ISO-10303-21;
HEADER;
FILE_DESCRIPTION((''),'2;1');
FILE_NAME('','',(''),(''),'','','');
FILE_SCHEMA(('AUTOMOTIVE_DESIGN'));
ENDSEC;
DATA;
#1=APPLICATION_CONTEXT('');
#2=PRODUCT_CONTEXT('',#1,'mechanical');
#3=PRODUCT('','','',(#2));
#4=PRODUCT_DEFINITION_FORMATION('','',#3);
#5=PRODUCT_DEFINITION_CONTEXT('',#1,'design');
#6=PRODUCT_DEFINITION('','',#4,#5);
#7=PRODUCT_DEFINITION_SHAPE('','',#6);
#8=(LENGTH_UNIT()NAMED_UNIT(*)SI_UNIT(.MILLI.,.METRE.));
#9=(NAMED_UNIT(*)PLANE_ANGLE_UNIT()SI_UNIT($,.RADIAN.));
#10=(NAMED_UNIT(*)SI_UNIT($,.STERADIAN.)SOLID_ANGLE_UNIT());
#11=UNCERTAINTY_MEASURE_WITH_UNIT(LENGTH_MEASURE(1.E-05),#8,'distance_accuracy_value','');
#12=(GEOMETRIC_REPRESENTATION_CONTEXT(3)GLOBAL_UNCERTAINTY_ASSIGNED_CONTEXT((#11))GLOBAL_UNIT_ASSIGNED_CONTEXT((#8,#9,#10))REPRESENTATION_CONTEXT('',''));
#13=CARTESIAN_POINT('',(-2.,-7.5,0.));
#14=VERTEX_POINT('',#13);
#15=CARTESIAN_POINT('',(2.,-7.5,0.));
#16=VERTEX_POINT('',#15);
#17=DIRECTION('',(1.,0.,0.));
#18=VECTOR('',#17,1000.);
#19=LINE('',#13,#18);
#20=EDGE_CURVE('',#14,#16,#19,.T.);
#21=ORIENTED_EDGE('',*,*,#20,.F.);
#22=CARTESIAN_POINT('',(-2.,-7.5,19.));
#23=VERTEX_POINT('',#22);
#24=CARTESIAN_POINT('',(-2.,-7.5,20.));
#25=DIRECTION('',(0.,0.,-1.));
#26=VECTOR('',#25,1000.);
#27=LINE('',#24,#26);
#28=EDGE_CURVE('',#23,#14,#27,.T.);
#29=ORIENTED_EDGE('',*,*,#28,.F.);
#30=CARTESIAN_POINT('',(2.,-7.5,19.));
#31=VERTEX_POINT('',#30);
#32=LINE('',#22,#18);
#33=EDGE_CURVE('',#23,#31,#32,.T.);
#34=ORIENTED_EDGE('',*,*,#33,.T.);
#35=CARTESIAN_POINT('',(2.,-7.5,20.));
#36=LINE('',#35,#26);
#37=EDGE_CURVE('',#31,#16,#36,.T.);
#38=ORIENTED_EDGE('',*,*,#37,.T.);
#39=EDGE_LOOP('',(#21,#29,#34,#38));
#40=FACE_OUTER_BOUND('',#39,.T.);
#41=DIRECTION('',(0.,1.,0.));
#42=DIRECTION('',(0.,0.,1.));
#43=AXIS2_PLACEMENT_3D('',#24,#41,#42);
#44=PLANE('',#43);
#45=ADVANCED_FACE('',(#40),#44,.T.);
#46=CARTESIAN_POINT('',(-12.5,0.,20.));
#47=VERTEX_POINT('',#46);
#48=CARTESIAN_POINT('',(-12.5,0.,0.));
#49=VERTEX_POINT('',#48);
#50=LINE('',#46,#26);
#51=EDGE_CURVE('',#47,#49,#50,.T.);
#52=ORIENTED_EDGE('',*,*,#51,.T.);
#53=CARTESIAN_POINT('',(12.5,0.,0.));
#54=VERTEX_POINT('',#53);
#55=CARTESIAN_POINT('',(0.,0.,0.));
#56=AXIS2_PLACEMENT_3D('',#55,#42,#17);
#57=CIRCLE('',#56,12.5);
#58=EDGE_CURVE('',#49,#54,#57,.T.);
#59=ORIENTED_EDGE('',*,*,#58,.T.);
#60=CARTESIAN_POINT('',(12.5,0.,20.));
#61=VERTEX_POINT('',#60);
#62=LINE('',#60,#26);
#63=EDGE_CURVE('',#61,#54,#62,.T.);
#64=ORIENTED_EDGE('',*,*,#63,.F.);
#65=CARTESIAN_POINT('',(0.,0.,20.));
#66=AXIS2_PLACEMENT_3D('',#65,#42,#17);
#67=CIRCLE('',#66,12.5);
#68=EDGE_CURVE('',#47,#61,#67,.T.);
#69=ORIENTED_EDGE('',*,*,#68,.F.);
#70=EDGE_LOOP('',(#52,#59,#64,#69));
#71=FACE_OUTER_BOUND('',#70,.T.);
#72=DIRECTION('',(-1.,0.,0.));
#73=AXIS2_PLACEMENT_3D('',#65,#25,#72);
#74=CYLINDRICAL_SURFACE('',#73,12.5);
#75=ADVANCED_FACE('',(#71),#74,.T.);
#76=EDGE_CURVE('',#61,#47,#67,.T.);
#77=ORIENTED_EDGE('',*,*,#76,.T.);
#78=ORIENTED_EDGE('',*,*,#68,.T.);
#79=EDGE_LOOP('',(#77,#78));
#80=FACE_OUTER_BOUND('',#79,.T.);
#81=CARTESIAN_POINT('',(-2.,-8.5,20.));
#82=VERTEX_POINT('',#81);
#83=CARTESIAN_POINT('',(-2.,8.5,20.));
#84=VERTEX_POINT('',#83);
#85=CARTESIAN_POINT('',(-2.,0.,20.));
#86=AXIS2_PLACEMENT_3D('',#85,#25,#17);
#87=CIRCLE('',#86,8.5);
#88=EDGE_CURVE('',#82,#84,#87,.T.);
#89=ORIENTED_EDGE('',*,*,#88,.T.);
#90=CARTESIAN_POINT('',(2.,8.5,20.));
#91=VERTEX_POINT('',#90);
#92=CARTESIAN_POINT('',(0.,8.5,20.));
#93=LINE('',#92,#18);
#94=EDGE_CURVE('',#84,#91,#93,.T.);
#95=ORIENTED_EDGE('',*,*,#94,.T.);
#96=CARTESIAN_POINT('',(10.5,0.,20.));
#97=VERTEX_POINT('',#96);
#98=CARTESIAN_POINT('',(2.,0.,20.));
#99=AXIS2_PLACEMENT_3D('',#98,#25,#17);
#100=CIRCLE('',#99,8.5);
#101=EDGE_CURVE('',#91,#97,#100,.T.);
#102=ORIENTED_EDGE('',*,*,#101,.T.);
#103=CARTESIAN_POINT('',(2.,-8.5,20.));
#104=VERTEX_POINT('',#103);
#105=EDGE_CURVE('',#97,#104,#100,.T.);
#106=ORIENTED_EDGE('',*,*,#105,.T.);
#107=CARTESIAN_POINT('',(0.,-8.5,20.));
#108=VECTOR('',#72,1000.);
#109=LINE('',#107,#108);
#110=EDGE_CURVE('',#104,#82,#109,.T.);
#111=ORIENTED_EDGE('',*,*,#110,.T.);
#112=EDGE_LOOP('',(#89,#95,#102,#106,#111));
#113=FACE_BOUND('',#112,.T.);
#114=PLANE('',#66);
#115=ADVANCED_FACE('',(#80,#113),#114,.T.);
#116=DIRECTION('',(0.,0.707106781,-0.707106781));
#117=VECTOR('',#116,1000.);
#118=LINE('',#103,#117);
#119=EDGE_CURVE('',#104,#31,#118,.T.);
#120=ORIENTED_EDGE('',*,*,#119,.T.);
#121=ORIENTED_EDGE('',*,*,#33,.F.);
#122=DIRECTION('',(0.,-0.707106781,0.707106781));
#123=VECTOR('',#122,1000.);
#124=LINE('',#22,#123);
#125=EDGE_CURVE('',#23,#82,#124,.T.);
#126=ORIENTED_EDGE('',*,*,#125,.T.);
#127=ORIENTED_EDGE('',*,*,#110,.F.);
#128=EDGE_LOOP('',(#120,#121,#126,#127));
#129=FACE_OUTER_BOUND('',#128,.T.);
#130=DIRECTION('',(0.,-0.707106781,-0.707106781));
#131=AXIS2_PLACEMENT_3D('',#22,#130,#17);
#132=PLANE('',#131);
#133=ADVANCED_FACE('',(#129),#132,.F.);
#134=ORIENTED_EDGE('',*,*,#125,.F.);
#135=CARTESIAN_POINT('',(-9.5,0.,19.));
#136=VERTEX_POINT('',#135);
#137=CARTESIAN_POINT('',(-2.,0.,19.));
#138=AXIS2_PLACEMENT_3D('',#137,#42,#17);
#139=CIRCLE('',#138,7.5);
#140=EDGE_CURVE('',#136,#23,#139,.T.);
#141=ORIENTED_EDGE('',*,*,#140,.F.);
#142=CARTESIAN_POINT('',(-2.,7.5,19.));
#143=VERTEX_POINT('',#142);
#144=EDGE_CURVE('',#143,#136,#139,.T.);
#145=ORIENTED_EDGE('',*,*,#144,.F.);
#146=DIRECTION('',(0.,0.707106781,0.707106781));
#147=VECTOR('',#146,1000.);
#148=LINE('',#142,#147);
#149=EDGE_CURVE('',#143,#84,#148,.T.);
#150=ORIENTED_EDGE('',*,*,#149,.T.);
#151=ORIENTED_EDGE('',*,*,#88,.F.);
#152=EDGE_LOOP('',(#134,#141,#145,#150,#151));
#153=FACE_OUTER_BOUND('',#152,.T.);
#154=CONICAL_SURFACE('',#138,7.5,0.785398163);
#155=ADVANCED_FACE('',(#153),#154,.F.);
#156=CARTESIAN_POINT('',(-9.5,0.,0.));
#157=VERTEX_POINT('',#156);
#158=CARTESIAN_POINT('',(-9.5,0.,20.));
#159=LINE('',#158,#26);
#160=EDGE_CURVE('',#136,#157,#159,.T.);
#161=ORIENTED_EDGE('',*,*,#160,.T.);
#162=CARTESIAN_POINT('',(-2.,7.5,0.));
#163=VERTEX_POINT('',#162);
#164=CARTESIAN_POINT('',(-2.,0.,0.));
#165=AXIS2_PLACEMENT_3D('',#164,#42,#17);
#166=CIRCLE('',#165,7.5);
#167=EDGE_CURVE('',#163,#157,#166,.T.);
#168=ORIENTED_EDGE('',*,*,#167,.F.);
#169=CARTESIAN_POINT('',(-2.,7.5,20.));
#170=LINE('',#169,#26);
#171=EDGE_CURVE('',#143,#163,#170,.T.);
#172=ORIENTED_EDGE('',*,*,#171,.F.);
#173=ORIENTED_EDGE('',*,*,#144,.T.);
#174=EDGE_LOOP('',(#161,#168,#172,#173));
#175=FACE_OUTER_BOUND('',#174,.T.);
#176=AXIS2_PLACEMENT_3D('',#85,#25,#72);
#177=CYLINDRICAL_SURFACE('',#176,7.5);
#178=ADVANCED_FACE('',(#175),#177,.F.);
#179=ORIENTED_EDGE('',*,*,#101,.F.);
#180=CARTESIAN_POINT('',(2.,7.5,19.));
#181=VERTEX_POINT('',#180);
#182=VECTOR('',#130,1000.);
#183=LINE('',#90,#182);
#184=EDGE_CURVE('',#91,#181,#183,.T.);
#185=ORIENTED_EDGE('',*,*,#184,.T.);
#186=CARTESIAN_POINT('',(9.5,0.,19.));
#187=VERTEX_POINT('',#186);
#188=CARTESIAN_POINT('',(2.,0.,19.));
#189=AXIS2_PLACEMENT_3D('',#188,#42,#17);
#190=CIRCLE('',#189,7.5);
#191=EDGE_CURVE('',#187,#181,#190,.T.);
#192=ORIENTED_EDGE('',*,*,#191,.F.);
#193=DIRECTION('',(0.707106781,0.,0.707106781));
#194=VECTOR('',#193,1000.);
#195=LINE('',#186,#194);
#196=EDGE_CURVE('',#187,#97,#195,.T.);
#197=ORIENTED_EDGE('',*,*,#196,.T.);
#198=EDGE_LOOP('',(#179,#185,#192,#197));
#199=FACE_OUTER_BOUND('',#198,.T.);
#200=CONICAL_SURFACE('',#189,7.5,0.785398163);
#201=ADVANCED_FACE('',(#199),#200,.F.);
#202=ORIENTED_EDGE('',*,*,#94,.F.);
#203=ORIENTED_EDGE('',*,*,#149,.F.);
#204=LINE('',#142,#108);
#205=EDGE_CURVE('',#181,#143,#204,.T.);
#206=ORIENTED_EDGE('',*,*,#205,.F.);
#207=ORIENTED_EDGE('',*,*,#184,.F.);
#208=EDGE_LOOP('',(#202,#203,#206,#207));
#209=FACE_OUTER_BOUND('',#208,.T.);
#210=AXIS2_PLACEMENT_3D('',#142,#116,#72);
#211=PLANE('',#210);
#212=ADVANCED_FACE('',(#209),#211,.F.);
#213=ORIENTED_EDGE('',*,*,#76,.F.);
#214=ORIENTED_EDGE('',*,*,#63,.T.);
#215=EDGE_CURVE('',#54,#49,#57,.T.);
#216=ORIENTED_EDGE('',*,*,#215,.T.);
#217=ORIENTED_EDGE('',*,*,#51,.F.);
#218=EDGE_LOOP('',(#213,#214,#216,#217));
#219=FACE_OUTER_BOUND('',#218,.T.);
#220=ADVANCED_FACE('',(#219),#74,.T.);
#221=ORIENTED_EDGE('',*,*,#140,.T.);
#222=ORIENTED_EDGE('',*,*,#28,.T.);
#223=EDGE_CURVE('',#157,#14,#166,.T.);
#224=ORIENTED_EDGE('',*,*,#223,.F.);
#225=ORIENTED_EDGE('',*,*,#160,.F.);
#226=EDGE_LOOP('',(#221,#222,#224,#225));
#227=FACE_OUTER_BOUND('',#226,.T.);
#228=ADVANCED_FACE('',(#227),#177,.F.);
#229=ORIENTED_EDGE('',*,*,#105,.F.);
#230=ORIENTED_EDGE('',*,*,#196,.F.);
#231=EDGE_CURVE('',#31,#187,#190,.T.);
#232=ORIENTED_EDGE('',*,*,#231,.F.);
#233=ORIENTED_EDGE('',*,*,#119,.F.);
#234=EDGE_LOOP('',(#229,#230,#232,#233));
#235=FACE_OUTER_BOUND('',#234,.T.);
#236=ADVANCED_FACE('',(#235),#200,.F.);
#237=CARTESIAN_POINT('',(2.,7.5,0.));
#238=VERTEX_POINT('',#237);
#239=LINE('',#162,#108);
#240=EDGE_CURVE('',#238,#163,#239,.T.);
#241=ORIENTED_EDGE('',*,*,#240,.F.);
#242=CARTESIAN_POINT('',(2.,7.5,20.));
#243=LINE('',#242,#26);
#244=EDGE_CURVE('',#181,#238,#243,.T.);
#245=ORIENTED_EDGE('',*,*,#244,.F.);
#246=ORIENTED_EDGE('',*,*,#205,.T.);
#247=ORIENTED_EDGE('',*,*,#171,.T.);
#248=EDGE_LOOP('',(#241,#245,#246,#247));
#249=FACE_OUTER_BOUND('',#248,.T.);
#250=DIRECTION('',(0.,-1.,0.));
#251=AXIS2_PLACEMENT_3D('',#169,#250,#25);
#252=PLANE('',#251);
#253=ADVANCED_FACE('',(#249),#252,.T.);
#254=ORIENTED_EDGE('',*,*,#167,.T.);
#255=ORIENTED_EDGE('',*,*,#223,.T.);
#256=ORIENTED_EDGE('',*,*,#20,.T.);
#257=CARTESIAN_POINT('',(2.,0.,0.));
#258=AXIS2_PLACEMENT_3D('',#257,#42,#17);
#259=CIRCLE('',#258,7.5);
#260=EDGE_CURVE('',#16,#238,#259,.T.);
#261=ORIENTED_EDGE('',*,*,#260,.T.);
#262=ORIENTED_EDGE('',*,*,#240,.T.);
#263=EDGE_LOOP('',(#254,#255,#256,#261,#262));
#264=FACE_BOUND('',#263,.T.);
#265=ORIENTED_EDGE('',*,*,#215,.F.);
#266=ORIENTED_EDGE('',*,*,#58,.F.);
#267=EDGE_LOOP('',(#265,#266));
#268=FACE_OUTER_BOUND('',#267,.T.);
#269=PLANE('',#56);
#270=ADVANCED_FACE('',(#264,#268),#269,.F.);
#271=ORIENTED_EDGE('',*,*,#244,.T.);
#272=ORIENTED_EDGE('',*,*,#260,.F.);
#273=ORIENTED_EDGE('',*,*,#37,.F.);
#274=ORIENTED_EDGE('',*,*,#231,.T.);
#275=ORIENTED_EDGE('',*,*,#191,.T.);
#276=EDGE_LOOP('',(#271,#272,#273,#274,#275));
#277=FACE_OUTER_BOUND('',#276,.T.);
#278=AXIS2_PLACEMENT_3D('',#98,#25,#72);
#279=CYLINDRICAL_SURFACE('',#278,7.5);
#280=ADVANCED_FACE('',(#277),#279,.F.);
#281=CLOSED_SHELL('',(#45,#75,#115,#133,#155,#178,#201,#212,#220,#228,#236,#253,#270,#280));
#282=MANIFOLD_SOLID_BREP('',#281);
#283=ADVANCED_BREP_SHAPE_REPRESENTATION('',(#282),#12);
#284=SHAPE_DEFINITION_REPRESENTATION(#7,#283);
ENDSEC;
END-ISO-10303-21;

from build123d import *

# Parameters (mm, degrees)
SKETCH1_R           = 12.5
BOSS_EXTRUDE1_DEPTH = 20
CHAMFER1_SIZE       = 1


with BuildPart() as part:
    # Sketch1 → Boss-Extrude1 (new body)
    with BuildSketch(Plane.XY):
        Circle(SKETCH1_R)
        with BuildLine():
            Line((-2, 7.5), (2, 7.5))
            ThreePointArc((2, 7.5), (9.5, 0), (2, -7.5))
            Line((2, -7.5), (-2, -7.5))
            ThreePointArc((-2, -7.5), (-9.5, 0), (-2, 7.5))
        make_face(mode=Mode.SUBTRACT)
    extrude(amount=BOSS_EXTRUDE1_DEPTH)

    # Chamfer1
    chamfer1_edges = [part.edges().sort_by_distance(p)[0] for p in [
        (0, 7.5, 20),
        (-9.5, 0, 20),
        (0, -7.5, 20),
        (9.5, 0, 20),
    ]]
    chamfer(chamfer1_edges, length=CHAMFER1_SIZE)


solid = part.part
